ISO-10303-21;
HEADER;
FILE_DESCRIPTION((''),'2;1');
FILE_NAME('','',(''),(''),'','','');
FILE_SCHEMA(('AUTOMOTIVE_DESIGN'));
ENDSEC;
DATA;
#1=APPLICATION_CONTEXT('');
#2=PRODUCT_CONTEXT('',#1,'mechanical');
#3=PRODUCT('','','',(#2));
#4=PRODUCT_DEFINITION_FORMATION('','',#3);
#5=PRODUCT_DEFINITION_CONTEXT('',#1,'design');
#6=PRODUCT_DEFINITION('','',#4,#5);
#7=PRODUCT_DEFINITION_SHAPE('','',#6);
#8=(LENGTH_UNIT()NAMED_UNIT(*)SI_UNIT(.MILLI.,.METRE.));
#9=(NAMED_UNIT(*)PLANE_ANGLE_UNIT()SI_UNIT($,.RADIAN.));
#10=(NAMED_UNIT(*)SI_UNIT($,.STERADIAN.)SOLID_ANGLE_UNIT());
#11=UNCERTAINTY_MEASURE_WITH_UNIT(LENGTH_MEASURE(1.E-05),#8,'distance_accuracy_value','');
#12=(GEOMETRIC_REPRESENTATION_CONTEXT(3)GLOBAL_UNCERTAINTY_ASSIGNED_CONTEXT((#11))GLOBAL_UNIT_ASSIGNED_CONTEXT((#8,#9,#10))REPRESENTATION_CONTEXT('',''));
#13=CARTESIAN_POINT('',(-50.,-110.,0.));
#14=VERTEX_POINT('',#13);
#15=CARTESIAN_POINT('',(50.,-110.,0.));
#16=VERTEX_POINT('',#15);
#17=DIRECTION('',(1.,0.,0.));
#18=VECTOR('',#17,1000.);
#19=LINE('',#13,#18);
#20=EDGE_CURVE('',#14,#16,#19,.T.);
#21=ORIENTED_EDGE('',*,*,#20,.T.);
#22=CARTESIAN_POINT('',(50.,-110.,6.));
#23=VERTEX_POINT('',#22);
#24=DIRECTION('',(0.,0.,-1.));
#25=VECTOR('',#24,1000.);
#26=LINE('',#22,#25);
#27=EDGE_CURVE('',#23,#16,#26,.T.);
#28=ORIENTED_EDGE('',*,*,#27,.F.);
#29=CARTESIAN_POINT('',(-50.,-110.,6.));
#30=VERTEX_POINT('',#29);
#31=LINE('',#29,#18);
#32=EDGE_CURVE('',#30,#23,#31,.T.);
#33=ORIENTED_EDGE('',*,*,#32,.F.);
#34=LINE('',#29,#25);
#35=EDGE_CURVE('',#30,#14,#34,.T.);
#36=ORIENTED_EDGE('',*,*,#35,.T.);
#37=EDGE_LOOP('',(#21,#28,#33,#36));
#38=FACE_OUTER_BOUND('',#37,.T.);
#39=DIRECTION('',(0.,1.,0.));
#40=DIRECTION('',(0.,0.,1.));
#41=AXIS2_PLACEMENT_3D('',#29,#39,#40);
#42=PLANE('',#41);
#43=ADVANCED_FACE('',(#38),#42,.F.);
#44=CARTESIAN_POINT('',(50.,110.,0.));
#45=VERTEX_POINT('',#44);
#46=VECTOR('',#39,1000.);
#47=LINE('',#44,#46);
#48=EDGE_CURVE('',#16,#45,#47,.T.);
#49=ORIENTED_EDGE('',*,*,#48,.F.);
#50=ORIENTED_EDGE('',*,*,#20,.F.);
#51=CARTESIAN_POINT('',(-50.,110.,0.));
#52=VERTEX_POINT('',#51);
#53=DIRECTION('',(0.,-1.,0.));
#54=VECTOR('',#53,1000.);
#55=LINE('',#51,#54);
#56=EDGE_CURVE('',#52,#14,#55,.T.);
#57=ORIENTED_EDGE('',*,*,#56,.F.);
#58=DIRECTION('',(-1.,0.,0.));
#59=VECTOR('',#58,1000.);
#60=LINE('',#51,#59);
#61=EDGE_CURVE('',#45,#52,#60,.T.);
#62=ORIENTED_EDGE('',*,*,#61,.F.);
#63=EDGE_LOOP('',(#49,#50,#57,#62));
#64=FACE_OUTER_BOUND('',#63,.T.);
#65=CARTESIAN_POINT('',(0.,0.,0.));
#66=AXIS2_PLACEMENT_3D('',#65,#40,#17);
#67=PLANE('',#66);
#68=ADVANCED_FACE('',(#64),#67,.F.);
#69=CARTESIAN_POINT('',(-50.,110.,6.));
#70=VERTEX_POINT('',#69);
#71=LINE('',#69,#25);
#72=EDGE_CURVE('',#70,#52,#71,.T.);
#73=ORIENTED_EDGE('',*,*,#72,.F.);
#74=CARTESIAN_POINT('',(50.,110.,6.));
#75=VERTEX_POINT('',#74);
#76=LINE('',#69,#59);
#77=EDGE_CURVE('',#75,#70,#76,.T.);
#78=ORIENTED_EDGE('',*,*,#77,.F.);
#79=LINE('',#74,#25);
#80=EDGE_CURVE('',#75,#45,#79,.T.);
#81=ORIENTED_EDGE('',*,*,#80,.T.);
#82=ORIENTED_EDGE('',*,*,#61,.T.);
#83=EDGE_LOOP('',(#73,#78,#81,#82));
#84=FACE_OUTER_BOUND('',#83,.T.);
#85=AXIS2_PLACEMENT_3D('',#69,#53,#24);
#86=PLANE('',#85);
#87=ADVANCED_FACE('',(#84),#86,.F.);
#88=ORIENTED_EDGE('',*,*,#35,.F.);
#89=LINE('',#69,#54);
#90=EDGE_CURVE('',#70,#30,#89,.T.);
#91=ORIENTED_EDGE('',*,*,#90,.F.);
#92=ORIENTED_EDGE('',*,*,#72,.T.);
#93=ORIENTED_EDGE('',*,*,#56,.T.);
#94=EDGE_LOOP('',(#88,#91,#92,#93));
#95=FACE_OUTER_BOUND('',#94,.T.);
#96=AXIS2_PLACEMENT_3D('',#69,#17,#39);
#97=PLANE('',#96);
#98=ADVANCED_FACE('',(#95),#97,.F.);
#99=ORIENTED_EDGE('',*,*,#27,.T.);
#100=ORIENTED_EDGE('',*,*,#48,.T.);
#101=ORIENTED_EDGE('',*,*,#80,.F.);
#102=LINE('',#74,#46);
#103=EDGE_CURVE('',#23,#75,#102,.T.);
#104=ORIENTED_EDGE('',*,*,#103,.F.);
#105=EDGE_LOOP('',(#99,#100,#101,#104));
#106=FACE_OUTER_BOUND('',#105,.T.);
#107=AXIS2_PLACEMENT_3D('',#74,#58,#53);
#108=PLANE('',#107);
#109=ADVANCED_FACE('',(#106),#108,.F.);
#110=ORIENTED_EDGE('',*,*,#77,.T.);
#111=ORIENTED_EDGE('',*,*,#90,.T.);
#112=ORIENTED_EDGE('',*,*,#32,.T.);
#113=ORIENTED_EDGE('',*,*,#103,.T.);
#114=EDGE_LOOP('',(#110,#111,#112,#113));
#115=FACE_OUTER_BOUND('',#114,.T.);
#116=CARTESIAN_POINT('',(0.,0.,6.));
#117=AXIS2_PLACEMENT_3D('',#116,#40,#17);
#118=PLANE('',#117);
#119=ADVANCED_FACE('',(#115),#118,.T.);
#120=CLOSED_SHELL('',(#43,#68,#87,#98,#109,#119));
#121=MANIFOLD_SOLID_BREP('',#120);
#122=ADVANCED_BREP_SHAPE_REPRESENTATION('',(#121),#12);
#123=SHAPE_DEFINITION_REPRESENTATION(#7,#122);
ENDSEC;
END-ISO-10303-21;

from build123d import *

# Parameters (mm, degrees)
SKETCH_1_W      = 100
SKETCH_1_H      = 220
EXTRUDE_1_DEPTH = 6


with BuildPart() as part:
    # 草图1 → 凸台-拉伸1 (new body)
    with BuildSketch(Plane.XY):
        Rectangle(SKETCH_1_W, SKETCH_1_H)
    extrude(amount=EXTRUDE_1_DEPTH)


solid = part.part
